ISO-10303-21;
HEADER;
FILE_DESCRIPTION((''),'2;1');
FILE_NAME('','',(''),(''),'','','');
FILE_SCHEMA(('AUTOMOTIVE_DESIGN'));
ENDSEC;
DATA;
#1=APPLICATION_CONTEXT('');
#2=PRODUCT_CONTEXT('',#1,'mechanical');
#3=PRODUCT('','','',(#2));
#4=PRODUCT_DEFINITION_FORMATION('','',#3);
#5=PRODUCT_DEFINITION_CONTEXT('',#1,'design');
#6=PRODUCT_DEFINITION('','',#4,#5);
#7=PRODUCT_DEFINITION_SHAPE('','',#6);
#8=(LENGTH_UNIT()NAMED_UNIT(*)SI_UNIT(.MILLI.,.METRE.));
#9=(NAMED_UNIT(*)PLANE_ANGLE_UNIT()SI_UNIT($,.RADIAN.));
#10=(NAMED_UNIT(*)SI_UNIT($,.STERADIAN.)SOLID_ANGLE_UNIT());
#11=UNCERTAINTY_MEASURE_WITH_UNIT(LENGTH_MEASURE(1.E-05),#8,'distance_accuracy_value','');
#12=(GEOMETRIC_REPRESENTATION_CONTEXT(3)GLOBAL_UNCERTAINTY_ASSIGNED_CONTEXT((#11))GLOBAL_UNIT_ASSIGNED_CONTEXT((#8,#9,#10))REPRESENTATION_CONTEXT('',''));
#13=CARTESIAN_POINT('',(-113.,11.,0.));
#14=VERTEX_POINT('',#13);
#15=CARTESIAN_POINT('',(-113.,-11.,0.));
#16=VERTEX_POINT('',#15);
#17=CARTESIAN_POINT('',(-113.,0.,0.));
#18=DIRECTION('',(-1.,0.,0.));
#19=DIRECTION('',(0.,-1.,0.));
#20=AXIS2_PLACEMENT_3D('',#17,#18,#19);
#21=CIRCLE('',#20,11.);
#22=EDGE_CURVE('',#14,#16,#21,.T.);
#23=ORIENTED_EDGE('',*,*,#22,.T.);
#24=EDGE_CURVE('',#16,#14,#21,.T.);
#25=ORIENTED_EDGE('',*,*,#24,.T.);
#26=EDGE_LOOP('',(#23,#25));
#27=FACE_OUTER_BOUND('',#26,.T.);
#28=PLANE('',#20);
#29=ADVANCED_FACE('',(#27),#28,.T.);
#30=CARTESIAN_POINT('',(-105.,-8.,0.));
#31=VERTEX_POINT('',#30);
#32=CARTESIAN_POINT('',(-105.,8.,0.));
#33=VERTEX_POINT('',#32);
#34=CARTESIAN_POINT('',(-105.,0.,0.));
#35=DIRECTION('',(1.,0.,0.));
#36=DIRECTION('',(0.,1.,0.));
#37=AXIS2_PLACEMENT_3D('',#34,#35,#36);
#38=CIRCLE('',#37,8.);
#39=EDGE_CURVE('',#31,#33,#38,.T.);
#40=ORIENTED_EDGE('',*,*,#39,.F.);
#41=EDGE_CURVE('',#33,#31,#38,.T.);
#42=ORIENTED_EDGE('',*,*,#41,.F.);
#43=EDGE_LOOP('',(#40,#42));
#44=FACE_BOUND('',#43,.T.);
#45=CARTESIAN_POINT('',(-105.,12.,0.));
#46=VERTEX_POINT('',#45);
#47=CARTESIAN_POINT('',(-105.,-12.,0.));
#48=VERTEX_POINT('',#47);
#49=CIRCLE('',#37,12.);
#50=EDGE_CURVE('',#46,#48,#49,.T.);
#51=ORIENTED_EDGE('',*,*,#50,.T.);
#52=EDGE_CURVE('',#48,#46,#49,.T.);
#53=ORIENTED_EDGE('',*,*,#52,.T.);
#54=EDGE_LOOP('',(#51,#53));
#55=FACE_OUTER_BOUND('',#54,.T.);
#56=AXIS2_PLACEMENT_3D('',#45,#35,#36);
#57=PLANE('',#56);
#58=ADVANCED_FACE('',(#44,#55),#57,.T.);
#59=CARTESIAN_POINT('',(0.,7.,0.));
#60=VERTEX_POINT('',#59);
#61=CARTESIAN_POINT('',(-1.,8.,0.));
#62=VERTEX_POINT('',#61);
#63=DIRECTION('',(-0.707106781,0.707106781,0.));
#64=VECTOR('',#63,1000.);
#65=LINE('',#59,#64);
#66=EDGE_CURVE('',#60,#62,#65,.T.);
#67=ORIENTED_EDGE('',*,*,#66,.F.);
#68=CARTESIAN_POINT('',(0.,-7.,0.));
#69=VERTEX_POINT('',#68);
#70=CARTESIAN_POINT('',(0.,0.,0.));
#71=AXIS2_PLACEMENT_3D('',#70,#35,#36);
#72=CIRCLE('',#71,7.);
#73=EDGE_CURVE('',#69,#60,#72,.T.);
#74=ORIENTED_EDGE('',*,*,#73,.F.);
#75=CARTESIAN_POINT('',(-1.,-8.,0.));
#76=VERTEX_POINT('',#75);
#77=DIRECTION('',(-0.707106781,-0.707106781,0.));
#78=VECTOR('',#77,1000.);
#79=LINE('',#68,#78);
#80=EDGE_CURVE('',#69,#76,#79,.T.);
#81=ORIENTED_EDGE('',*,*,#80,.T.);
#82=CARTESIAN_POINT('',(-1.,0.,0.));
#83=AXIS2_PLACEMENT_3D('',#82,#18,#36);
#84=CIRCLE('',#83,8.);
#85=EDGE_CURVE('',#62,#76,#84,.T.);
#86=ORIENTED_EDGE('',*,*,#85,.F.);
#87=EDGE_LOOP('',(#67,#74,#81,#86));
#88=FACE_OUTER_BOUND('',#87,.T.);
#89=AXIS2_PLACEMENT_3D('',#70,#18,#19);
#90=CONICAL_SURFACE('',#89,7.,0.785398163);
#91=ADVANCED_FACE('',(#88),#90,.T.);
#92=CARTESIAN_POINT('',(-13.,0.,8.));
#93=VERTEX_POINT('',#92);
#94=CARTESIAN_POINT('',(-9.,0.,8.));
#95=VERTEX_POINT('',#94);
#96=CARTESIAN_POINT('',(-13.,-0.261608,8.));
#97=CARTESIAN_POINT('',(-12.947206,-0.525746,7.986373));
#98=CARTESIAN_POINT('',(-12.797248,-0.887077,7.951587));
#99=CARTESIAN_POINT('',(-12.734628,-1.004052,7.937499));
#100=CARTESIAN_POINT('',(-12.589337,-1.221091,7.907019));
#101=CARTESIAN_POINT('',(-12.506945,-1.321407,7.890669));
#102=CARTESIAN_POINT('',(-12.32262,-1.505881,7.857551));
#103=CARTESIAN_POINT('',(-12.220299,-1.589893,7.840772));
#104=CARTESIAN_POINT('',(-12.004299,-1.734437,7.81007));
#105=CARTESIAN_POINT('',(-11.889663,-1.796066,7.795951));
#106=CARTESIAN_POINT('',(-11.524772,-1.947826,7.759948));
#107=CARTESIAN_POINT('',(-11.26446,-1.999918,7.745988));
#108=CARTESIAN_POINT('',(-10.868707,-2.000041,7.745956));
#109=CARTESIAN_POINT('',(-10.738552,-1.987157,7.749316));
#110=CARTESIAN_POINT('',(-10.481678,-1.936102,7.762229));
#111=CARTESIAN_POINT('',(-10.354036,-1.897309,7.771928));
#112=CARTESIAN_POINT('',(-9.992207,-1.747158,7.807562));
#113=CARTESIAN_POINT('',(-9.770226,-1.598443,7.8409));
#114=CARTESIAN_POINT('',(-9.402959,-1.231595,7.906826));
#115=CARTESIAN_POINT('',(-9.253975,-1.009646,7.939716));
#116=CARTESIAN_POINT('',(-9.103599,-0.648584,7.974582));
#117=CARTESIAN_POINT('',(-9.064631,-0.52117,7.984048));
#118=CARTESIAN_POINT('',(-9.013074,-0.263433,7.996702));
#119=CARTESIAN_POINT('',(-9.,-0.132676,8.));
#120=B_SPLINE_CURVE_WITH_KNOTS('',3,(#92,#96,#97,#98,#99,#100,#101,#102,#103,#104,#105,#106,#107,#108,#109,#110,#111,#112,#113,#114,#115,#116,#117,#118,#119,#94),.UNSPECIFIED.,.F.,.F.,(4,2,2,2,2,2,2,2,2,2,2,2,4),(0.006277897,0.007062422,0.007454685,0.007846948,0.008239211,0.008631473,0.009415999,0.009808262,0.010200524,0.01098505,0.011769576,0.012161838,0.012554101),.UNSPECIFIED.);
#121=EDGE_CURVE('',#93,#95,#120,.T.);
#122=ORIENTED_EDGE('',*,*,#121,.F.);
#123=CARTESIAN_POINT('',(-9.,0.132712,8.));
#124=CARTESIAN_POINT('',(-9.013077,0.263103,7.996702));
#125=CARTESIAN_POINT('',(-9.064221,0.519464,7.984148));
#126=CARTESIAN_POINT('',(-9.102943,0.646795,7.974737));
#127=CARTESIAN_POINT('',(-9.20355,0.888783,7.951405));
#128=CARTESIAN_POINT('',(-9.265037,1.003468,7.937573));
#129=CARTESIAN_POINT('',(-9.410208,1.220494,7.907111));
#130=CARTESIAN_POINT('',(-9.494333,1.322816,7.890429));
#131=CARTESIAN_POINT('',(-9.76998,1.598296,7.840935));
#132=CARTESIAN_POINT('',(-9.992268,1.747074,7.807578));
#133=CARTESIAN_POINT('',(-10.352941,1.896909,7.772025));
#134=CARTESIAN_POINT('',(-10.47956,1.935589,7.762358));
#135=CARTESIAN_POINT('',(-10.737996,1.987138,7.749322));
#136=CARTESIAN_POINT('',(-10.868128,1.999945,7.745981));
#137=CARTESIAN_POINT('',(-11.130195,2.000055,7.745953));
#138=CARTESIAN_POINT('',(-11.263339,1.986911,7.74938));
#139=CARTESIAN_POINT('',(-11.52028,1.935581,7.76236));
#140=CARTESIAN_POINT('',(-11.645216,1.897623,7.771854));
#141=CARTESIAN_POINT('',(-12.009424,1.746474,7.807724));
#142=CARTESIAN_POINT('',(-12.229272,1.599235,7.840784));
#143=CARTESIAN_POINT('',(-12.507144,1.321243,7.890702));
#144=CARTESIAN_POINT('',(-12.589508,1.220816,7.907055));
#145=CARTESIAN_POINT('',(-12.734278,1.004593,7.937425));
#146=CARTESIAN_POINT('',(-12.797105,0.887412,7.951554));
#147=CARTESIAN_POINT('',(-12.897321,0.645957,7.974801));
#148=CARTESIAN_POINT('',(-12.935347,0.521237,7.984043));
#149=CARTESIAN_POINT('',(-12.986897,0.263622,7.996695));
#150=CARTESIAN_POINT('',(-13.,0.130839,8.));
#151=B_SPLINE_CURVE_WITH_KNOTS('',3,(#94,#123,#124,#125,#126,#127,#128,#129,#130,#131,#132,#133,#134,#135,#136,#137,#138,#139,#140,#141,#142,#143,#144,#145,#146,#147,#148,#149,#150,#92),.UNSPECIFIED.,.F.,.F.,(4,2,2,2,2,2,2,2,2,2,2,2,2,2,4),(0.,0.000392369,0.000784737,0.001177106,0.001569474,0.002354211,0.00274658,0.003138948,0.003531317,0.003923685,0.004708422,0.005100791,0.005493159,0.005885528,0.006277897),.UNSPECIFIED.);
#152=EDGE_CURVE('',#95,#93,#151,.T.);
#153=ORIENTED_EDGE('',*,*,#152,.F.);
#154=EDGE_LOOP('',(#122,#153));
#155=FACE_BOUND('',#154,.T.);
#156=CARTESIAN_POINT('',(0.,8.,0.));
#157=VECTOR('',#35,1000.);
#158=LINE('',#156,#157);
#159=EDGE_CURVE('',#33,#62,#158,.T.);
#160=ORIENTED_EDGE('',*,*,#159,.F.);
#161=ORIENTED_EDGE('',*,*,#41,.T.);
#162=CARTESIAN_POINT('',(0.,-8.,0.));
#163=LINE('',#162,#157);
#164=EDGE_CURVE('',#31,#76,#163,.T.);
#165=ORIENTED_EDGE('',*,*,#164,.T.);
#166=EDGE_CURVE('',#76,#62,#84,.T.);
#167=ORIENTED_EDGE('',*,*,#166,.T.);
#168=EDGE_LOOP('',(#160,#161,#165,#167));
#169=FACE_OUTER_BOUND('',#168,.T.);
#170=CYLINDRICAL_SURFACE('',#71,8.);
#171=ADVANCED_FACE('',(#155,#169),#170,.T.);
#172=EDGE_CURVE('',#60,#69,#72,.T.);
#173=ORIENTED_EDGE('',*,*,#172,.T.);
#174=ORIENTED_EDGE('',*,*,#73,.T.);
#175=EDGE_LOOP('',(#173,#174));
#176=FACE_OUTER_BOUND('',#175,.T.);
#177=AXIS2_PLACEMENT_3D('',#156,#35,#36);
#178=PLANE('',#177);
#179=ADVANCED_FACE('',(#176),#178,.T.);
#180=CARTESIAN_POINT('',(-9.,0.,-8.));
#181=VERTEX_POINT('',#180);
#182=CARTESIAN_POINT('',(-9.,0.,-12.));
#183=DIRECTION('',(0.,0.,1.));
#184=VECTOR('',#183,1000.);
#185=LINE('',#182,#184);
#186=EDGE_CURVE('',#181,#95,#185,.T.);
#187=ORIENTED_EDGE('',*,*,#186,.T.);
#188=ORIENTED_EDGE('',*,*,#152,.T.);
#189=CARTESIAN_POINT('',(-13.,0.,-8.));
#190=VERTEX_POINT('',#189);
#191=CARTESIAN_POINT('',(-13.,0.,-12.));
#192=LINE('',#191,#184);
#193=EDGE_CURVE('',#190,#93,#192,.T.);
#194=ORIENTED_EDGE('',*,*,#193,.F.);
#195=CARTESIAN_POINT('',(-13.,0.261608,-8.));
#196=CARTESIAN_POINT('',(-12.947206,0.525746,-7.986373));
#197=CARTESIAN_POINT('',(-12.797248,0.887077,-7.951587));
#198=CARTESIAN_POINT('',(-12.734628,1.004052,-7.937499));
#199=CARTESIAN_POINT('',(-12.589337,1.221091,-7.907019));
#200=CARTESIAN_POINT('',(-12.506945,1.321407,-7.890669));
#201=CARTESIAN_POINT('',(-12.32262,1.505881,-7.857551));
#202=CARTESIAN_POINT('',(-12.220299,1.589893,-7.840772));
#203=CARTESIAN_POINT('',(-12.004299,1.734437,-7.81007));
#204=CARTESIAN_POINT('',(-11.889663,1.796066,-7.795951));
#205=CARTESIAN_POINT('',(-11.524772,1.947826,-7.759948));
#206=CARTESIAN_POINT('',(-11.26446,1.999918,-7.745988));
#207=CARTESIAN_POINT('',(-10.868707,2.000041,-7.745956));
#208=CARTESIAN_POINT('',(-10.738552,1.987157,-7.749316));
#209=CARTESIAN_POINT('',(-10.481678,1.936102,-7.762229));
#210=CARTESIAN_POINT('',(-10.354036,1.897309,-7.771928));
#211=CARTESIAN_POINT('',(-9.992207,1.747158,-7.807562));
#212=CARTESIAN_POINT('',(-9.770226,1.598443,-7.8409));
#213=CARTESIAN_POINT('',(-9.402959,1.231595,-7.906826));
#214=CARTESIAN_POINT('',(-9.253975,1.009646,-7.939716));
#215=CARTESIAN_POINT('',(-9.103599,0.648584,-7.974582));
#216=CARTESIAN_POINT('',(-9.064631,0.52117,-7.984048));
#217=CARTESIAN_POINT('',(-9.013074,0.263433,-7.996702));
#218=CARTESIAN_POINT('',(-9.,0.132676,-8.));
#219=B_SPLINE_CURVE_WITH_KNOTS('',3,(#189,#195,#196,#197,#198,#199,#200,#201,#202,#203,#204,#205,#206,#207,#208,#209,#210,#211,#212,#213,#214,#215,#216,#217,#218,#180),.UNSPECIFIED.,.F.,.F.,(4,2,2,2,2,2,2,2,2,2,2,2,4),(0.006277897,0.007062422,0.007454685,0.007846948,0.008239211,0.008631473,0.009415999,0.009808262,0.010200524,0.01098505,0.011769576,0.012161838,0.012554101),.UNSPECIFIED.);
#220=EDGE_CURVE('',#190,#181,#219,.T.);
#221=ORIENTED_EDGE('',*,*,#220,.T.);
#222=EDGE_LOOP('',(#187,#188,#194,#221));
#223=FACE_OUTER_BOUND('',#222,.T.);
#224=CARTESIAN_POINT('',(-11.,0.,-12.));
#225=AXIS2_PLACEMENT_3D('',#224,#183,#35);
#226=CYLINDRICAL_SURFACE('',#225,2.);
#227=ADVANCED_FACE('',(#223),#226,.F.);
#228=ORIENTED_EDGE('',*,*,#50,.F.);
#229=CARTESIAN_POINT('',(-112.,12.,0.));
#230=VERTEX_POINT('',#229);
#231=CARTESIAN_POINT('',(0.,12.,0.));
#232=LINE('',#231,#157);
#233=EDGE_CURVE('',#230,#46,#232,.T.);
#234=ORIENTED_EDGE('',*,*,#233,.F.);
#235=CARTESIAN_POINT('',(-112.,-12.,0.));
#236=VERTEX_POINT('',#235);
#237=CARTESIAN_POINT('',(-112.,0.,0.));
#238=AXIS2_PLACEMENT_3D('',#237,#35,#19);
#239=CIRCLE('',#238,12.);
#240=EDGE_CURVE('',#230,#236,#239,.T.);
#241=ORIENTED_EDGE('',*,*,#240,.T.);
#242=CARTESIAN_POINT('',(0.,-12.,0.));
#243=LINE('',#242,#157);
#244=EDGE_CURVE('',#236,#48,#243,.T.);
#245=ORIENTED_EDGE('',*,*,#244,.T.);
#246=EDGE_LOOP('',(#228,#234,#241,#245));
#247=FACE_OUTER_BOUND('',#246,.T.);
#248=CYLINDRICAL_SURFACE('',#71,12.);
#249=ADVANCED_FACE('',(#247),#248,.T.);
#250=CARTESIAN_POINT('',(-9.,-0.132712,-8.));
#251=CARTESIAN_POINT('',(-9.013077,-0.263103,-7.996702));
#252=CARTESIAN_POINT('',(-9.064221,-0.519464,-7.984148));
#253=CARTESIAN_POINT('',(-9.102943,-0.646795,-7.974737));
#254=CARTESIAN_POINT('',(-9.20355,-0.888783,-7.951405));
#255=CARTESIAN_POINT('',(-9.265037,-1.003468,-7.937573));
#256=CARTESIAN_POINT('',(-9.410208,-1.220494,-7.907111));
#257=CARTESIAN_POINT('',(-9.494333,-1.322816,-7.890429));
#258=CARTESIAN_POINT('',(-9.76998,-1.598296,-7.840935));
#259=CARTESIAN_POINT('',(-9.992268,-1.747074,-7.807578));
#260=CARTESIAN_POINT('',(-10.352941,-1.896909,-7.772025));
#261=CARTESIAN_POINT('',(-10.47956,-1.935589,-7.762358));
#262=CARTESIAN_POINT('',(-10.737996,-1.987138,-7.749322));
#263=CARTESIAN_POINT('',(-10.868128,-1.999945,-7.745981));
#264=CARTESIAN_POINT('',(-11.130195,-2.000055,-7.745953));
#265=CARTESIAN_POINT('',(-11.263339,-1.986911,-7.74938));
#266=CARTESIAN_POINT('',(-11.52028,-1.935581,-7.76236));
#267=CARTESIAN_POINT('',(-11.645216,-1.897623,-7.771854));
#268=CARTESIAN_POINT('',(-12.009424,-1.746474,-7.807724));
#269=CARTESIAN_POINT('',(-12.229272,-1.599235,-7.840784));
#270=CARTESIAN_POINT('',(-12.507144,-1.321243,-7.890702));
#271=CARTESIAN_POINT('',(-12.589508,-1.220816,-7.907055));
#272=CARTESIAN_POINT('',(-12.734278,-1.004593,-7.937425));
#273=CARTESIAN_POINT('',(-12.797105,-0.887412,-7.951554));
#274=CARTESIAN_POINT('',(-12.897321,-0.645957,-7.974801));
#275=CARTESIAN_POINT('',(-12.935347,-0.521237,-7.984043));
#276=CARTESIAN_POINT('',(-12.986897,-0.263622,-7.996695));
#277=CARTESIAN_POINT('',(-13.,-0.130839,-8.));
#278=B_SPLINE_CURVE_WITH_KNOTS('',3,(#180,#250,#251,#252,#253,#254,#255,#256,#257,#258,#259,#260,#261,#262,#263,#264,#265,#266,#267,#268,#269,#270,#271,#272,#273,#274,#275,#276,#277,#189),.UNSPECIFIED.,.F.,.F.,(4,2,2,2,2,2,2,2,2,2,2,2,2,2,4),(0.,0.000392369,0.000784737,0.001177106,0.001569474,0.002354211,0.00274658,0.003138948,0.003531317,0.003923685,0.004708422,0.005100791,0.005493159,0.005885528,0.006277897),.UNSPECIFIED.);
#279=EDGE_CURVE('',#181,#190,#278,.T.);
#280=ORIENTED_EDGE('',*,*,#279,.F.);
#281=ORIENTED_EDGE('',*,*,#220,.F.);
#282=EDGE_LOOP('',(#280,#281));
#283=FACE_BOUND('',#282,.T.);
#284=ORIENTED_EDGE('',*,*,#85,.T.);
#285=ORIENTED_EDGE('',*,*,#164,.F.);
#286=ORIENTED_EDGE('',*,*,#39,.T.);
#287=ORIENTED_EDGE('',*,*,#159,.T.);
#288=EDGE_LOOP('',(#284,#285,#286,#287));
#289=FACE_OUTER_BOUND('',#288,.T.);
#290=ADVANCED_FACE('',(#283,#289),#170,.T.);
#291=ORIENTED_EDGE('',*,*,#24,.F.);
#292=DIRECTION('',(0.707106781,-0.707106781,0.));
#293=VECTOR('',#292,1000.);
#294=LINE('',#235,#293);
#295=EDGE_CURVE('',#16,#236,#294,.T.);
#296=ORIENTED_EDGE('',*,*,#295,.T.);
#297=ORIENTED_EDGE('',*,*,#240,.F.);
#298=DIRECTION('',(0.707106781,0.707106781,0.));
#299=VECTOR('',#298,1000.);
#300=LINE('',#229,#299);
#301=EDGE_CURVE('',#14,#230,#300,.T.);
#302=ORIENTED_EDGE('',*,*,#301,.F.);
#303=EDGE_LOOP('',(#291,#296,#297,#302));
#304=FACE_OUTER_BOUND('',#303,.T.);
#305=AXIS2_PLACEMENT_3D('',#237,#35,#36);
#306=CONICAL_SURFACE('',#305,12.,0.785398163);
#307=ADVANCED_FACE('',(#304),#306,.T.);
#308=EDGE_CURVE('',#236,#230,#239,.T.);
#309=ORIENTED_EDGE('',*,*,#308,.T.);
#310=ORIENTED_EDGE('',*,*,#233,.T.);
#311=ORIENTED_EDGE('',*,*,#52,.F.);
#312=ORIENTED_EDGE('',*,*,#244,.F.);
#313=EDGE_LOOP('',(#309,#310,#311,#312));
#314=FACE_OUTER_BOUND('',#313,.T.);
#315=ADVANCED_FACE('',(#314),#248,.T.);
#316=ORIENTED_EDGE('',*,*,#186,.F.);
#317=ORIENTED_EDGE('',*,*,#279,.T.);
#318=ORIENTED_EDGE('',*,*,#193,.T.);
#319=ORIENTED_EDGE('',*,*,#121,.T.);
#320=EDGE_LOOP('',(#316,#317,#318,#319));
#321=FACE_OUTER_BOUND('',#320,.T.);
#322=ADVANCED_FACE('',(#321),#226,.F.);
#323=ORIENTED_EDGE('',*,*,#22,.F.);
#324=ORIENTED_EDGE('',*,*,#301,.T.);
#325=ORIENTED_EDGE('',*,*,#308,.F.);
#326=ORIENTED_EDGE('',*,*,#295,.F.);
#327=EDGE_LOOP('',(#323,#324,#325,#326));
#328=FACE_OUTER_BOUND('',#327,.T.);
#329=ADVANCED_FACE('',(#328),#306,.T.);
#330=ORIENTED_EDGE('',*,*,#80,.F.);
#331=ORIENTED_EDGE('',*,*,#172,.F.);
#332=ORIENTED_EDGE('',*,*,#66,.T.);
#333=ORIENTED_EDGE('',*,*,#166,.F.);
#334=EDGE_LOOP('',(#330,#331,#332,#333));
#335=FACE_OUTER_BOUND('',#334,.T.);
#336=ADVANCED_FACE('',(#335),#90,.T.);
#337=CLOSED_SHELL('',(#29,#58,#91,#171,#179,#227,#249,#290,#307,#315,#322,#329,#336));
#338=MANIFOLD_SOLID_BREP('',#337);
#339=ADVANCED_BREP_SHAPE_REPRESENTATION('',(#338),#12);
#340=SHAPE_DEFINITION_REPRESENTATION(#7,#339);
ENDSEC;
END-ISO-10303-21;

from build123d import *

# Parameters (mm, degrees)
CUT_EXTRUDE1_DEPTH      = 115.267230648
CUT_EXTRUDE1_DEPTH_BACK = 115.267230648
SKETCH2_R               = 2
CHAMFER1_SIZE           = 1
CHAMFER2_SIZE           = 1


with BuildPart() as part:
    # Sketch1 → Revolve1 (revolve)
    with BuildSketch(Plane.XY):
        Polygon((0, 0), (-113, 0), (-113, 12), (-105, 12), (-105, 8), (0, 8), align=None)
    revolve(axis=Axis((0, 0, 0), (-1, 0, 0)))

    # Sketch2 → Cut-Extrude1 (cut, two sides: drawn at the far end of the back side and taken through both)
    with BuildSketch(Plane.XY.offset(-CUT_EXTRUDE1_DEPTH_BACK)):
        with Locations((-11, 0)):
            Circle(SKETCH2_R)
    extrude(amount=CUT_EXTRUDE1_DEPTH + CUT_EXTRUDE1_DEPTH_BACK, mode=Mode.SUBTRACT)

    # Chamfer1
    chamfer1_edges = [part.edges().sort_by_distance(p)[0] for p in [
        (0, -8, 0),
    ]]
    chamfer(chamfer1_edges, length=CHAMFER1_SIZE)

    # Chamfer2
    chamfer2_edges = [part.edges().sort_by_distance(p)[0] for p in [
        (-113, -12, 0),
    ]]
    chamfer(chamfer2_edges, length=CHAMFER2_SIZE)


solid = part.part
